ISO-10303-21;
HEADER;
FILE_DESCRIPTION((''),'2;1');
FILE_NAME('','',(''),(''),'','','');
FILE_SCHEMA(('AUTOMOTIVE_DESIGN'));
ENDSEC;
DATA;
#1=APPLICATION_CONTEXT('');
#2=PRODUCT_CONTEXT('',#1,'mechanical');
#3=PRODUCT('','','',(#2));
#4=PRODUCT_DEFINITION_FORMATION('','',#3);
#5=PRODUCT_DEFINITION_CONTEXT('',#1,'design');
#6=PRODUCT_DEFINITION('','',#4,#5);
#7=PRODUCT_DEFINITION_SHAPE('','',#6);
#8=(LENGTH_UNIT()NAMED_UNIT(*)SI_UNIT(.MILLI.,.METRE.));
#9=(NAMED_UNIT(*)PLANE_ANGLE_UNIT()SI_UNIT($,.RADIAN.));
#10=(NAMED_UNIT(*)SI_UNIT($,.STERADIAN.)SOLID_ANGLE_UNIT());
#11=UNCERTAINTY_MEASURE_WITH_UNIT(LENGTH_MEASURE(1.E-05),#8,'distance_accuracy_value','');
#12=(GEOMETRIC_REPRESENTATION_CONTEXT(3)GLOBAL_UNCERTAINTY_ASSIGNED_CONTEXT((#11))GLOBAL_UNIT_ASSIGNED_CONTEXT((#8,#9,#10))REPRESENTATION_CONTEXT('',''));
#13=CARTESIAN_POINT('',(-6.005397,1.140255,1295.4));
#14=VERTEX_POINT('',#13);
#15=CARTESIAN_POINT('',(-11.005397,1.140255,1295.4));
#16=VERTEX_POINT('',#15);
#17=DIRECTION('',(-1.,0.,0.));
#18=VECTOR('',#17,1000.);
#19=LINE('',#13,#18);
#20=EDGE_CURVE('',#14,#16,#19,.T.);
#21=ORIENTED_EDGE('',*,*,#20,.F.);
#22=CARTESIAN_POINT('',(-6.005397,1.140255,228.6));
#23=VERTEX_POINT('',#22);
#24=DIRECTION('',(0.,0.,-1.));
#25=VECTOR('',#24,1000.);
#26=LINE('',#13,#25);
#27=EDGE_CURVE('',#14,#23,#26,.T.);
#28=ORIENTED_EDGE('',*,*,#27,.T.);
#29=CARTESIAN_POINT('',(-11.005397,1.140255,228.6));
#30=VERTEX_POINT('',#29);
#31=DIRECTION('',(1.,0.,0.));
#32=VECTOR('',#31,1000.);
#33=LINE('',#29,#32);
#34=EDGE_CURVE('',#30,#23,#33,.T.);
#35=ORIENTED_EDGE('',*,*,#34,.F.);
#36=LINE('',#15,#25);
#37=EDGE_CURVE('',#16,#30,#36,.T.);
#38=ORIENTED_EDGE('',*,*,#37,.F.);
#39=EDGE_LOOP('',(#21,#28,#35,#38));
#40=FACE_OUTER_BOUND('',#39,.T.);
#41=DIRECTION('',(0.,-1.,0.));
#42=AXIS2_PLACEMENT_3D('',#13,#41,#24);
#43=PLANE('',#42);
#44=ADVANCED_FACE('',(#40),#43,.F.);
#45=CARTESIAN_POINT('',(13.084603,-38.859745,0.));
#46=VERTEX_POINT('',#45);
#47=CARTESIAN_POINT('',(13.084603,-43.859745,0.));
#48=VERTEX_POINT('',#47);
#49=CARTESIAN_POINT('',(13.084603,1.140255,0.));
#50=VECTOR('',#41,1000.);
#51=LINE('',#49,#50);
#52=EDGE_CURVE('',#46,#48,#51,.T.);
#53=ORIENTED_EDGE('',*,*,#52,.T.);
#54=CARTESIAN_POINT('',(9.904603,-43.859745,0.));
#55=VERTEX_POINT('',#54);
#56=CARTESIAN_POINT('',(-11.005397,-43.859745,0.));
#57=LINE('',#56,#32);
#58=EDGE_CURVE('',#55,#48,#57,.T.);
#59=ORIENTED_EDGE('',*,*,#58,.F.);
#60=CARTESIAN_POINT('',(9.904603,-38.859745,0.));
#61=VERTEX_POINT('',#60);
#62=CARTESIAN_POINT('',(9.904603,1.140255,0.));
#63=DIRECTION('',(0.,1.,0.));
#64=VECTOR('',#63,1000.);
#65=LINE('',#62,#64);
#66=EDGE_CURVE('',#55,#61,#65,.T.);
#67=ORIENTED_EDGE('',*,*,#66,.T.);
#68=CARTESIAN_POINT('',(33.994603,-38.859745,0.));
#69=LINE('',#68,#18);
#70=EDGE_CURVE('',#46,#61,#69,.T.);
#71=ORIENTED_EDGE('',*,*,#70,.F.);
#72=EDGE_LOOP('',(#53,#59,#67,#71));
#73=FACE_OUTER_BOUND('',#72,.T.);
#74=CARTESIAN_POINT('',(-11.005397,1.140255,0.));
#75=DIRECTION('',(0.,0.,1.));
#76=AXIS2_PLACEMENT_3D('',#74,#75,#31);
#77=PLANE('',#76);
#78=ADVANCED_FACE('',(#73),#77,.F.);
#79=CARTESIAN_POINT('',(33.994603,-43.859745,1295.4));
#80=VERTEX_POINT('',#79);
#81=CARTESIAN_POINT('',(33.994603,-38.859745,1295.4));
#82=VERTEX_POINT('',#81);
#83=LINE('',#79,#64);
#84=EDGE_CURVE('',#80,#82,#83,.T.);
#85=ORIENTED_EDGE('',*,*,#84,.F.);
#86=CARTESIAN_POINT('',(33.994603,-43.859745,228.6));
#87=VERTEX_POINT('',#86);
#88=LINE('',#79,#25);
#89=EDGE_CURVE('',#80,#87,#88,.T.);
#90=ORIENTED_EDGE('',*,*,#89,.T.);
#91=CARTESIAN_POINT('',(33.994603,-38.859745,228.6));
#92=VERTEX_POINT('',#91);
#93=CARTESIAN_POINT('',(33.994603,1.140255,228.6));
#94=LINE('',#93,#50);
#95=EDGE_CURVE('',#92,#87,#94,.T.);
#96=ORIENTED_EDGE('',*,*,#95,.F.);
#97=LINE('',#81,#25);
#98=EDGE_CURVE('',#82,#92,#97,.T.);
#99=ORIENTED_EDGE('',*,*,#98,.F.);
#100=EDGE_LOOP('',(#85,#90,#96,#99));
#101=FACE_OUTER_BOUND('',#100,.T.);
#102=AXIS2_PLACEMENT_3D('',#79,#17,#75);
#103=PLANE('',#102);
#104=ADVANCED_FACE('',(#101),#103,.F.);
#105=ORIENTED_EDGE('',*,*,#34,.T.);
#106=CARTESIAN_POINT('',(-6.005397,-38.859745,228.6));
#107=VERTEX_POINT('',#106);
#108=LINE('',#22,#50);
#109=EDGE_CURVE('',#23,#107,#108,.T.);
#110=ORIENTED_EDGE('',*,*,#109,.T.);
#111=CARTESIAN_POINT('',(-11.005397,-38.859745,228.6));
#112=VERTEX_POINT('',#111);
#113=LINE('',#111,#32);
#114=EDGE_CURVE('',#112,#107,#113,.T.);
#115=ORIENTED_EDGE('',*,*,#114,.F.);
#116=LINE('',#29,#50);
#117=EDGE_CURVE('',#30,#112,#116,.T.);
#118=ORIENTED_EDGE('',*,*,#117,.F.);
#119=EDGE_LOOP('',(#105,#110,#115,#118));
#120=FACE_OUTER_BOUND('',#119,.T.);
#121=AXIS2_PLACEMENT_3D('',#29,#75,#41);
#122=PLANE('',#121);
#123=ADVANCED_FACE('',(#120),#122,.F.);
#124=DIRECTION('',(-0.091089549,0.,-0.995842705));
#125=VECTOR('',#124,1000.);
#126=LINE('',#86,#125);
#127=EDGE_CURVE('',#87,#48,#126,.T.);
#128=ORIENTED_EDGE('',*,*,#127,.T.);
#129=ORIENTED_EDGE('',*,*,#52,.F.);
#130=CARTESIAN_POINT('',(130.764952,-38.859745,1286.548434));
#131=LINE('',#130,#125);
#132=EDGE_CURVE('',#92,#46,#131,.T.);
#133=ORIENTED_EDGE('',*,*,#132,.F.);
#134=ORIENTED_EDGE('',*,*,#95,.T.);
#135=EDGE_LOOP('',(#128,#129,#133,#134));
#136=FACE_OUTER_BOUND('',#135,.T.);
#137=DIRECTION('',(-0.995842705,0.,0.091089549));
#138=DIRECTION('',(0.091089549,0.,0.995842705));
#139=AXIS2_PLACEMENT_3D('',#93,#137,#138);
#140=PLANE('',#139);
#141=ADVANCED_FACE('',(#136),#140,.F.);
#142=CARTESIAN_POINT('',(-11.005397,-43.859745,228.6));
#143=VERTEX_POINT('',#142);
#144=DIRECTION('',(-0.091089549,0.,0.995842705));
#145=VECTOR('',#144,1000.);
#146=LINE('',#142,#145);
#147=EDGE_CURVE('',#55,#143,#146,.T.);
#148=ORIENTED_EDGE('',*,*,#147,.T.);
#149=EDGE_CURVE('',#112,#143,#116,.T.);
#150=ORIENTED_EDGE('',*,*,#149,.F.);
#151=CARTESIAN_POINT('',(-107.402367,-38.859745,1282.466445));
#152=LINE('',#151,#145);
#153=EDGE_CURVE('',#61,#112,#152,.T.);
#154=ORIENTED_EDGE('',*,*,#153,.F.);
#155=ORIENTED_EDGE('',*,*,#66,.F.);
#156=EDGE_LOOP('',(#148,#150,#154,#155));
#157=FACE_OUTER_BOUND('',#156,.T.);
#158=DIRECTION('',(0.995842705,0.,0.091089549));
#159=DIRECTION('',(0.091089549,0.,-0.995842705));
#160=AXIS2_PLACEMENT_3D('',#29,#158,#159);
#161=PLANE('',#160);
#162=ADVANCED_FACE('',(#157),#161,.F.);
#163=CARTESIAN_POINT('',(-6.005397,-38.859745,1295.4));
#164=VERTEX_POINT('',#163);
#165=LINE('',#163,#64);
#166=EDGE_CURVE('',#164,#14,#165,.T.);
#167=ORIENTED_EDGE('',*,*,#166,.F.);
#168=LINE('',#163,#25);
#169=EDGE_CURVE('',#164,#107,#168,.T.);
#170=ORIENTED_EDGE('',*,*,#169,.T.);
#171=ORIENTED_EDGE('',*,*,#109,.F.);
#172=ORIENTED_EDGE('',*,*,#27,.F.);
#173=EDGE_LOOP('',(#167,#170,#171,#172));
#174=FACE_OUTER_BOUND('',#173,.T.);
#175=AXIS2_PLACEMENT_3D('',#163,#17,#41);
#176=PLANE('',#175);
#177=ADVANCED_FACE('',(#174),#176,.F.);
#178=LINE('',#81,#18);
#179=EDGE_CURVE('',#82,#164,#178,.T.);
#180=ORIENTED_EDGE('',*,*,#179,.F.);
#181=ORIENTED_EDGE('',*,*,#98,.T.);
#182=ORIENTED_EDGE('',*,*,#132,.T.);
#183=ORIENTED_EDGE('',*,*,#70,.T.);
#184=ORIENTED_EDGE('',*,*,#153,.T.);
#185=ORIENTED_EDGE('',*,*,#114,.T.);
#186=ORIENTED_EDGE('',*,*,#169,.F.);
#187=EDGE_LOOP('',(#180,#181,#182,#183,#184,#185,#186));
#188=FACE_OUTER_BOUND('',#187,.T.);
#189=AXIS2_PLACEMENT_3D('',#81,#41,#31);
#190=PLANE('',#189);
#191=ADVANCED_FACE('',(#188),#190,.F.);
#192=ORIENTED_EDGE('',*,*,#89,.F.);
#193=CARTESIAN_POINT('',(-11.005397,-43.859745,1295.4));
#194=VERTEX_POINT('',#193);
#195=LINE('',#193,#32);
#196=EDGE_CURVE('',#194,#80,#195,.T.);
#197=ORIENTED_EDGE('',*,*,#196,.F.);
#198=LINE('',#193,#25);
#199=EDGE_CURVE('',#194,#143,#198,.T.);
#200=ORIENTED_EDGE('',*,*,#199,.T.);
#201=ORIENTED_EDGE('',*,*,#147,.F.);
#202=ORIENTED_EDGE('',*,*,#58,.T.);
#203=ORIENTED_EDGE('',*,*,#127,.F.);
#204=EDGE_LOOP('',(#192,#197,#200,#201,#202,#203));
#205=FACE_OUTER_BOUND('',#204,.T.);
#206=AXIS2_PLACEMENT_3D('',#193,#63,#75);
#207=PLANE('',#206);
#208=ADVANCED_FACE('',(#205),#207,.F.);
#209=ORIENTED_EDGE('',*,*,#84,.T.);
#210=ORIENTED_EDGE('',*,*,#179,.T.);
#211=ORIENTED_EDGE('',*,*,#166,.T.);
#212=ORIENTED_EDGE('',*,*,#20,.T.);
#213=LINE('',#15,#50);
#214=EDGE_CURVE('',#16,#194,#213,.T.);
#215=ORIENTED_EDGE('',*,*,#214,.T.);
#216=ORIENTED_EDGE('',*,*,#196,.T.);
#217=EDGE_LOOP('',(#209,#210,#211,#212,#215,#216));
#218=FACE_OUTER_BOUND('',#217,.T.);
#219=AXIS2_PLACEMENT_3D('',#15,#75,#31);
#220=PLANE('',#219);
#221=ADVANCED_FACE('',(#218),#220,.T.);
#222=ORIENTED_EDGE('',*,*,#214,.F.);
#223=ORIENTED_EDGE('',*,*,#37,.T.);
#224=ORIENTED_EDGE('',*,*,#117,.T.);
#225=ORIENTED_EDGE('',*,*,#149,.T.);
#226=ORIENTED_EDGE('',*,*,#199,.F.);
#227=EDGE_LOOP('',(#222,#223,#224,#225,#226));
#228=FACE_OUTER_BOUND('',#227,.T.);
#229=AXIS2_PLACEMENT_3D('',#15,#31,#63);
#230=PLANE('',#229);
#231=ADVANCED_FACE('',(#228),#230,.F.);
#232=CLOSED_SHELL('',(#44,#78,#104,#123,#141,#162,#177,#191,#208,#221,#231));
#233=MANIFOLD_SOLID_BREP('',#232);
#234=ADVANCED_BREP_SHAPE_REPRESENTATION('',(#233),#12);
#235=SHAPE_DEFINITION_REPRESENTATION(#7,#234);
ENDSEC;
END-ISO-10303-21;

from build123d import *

# Parameters (mm, degrees)
EXTRUDE1_DEPTH = 1295.4
EXTRUDE2_DEPTH = 1297.627083248
SKETCH5_W      = 54.662840746
SKETCH5_H      = 40
EXTRUDE3_DEPTH = 1297.759359805


with BuildPart() as part:
    # Sketch1 → Extrude1 (new body)
    with BuildSketch(Plane.XY):
        Polygon((-11.005397301, 1.140254873), (-11.005397301, -43.859745127), (33.994602699, -43.859745127), (33.994602699, -38.859745127), (-6.005397301, -38.859745127), (-6.005397301, 1.140254873), align=None)
    extrude(amount=EXTRUDE1_DEPTH)

    # Sketch2 → Extrude2 (cut, through all)
    with BuildSketch(Plane.XZ.offset(43.859745127)):
        Polygon((-11.005397301, 0), (9.904602699, 0), (-11.005397301, 228.6), align=None)
        Polygon((33.994602699, 228.6), (13.084602699, 0), (33.994602699, 0), align=None)
    extrude(amount=-EXTRUDE2_DEPTH, mode=Mode.SUBTRACT)

    # Sketch5 → Extrude3 (cut, through all)
    with BuildSketch(Plane(origin=(-6.005397301, 0, 0), x_dir=(0, 0, -1), z_dir=(1, 0, 0))):
        with Locations((-201.268579627, -18.859745127)):
            Rectangle(SKETCH5_W, SKETCH5_H)
    extrude(amount=-EXTRUDE3_DEPTH, mode=Mode.SUBTRACT)


solid = part.part
